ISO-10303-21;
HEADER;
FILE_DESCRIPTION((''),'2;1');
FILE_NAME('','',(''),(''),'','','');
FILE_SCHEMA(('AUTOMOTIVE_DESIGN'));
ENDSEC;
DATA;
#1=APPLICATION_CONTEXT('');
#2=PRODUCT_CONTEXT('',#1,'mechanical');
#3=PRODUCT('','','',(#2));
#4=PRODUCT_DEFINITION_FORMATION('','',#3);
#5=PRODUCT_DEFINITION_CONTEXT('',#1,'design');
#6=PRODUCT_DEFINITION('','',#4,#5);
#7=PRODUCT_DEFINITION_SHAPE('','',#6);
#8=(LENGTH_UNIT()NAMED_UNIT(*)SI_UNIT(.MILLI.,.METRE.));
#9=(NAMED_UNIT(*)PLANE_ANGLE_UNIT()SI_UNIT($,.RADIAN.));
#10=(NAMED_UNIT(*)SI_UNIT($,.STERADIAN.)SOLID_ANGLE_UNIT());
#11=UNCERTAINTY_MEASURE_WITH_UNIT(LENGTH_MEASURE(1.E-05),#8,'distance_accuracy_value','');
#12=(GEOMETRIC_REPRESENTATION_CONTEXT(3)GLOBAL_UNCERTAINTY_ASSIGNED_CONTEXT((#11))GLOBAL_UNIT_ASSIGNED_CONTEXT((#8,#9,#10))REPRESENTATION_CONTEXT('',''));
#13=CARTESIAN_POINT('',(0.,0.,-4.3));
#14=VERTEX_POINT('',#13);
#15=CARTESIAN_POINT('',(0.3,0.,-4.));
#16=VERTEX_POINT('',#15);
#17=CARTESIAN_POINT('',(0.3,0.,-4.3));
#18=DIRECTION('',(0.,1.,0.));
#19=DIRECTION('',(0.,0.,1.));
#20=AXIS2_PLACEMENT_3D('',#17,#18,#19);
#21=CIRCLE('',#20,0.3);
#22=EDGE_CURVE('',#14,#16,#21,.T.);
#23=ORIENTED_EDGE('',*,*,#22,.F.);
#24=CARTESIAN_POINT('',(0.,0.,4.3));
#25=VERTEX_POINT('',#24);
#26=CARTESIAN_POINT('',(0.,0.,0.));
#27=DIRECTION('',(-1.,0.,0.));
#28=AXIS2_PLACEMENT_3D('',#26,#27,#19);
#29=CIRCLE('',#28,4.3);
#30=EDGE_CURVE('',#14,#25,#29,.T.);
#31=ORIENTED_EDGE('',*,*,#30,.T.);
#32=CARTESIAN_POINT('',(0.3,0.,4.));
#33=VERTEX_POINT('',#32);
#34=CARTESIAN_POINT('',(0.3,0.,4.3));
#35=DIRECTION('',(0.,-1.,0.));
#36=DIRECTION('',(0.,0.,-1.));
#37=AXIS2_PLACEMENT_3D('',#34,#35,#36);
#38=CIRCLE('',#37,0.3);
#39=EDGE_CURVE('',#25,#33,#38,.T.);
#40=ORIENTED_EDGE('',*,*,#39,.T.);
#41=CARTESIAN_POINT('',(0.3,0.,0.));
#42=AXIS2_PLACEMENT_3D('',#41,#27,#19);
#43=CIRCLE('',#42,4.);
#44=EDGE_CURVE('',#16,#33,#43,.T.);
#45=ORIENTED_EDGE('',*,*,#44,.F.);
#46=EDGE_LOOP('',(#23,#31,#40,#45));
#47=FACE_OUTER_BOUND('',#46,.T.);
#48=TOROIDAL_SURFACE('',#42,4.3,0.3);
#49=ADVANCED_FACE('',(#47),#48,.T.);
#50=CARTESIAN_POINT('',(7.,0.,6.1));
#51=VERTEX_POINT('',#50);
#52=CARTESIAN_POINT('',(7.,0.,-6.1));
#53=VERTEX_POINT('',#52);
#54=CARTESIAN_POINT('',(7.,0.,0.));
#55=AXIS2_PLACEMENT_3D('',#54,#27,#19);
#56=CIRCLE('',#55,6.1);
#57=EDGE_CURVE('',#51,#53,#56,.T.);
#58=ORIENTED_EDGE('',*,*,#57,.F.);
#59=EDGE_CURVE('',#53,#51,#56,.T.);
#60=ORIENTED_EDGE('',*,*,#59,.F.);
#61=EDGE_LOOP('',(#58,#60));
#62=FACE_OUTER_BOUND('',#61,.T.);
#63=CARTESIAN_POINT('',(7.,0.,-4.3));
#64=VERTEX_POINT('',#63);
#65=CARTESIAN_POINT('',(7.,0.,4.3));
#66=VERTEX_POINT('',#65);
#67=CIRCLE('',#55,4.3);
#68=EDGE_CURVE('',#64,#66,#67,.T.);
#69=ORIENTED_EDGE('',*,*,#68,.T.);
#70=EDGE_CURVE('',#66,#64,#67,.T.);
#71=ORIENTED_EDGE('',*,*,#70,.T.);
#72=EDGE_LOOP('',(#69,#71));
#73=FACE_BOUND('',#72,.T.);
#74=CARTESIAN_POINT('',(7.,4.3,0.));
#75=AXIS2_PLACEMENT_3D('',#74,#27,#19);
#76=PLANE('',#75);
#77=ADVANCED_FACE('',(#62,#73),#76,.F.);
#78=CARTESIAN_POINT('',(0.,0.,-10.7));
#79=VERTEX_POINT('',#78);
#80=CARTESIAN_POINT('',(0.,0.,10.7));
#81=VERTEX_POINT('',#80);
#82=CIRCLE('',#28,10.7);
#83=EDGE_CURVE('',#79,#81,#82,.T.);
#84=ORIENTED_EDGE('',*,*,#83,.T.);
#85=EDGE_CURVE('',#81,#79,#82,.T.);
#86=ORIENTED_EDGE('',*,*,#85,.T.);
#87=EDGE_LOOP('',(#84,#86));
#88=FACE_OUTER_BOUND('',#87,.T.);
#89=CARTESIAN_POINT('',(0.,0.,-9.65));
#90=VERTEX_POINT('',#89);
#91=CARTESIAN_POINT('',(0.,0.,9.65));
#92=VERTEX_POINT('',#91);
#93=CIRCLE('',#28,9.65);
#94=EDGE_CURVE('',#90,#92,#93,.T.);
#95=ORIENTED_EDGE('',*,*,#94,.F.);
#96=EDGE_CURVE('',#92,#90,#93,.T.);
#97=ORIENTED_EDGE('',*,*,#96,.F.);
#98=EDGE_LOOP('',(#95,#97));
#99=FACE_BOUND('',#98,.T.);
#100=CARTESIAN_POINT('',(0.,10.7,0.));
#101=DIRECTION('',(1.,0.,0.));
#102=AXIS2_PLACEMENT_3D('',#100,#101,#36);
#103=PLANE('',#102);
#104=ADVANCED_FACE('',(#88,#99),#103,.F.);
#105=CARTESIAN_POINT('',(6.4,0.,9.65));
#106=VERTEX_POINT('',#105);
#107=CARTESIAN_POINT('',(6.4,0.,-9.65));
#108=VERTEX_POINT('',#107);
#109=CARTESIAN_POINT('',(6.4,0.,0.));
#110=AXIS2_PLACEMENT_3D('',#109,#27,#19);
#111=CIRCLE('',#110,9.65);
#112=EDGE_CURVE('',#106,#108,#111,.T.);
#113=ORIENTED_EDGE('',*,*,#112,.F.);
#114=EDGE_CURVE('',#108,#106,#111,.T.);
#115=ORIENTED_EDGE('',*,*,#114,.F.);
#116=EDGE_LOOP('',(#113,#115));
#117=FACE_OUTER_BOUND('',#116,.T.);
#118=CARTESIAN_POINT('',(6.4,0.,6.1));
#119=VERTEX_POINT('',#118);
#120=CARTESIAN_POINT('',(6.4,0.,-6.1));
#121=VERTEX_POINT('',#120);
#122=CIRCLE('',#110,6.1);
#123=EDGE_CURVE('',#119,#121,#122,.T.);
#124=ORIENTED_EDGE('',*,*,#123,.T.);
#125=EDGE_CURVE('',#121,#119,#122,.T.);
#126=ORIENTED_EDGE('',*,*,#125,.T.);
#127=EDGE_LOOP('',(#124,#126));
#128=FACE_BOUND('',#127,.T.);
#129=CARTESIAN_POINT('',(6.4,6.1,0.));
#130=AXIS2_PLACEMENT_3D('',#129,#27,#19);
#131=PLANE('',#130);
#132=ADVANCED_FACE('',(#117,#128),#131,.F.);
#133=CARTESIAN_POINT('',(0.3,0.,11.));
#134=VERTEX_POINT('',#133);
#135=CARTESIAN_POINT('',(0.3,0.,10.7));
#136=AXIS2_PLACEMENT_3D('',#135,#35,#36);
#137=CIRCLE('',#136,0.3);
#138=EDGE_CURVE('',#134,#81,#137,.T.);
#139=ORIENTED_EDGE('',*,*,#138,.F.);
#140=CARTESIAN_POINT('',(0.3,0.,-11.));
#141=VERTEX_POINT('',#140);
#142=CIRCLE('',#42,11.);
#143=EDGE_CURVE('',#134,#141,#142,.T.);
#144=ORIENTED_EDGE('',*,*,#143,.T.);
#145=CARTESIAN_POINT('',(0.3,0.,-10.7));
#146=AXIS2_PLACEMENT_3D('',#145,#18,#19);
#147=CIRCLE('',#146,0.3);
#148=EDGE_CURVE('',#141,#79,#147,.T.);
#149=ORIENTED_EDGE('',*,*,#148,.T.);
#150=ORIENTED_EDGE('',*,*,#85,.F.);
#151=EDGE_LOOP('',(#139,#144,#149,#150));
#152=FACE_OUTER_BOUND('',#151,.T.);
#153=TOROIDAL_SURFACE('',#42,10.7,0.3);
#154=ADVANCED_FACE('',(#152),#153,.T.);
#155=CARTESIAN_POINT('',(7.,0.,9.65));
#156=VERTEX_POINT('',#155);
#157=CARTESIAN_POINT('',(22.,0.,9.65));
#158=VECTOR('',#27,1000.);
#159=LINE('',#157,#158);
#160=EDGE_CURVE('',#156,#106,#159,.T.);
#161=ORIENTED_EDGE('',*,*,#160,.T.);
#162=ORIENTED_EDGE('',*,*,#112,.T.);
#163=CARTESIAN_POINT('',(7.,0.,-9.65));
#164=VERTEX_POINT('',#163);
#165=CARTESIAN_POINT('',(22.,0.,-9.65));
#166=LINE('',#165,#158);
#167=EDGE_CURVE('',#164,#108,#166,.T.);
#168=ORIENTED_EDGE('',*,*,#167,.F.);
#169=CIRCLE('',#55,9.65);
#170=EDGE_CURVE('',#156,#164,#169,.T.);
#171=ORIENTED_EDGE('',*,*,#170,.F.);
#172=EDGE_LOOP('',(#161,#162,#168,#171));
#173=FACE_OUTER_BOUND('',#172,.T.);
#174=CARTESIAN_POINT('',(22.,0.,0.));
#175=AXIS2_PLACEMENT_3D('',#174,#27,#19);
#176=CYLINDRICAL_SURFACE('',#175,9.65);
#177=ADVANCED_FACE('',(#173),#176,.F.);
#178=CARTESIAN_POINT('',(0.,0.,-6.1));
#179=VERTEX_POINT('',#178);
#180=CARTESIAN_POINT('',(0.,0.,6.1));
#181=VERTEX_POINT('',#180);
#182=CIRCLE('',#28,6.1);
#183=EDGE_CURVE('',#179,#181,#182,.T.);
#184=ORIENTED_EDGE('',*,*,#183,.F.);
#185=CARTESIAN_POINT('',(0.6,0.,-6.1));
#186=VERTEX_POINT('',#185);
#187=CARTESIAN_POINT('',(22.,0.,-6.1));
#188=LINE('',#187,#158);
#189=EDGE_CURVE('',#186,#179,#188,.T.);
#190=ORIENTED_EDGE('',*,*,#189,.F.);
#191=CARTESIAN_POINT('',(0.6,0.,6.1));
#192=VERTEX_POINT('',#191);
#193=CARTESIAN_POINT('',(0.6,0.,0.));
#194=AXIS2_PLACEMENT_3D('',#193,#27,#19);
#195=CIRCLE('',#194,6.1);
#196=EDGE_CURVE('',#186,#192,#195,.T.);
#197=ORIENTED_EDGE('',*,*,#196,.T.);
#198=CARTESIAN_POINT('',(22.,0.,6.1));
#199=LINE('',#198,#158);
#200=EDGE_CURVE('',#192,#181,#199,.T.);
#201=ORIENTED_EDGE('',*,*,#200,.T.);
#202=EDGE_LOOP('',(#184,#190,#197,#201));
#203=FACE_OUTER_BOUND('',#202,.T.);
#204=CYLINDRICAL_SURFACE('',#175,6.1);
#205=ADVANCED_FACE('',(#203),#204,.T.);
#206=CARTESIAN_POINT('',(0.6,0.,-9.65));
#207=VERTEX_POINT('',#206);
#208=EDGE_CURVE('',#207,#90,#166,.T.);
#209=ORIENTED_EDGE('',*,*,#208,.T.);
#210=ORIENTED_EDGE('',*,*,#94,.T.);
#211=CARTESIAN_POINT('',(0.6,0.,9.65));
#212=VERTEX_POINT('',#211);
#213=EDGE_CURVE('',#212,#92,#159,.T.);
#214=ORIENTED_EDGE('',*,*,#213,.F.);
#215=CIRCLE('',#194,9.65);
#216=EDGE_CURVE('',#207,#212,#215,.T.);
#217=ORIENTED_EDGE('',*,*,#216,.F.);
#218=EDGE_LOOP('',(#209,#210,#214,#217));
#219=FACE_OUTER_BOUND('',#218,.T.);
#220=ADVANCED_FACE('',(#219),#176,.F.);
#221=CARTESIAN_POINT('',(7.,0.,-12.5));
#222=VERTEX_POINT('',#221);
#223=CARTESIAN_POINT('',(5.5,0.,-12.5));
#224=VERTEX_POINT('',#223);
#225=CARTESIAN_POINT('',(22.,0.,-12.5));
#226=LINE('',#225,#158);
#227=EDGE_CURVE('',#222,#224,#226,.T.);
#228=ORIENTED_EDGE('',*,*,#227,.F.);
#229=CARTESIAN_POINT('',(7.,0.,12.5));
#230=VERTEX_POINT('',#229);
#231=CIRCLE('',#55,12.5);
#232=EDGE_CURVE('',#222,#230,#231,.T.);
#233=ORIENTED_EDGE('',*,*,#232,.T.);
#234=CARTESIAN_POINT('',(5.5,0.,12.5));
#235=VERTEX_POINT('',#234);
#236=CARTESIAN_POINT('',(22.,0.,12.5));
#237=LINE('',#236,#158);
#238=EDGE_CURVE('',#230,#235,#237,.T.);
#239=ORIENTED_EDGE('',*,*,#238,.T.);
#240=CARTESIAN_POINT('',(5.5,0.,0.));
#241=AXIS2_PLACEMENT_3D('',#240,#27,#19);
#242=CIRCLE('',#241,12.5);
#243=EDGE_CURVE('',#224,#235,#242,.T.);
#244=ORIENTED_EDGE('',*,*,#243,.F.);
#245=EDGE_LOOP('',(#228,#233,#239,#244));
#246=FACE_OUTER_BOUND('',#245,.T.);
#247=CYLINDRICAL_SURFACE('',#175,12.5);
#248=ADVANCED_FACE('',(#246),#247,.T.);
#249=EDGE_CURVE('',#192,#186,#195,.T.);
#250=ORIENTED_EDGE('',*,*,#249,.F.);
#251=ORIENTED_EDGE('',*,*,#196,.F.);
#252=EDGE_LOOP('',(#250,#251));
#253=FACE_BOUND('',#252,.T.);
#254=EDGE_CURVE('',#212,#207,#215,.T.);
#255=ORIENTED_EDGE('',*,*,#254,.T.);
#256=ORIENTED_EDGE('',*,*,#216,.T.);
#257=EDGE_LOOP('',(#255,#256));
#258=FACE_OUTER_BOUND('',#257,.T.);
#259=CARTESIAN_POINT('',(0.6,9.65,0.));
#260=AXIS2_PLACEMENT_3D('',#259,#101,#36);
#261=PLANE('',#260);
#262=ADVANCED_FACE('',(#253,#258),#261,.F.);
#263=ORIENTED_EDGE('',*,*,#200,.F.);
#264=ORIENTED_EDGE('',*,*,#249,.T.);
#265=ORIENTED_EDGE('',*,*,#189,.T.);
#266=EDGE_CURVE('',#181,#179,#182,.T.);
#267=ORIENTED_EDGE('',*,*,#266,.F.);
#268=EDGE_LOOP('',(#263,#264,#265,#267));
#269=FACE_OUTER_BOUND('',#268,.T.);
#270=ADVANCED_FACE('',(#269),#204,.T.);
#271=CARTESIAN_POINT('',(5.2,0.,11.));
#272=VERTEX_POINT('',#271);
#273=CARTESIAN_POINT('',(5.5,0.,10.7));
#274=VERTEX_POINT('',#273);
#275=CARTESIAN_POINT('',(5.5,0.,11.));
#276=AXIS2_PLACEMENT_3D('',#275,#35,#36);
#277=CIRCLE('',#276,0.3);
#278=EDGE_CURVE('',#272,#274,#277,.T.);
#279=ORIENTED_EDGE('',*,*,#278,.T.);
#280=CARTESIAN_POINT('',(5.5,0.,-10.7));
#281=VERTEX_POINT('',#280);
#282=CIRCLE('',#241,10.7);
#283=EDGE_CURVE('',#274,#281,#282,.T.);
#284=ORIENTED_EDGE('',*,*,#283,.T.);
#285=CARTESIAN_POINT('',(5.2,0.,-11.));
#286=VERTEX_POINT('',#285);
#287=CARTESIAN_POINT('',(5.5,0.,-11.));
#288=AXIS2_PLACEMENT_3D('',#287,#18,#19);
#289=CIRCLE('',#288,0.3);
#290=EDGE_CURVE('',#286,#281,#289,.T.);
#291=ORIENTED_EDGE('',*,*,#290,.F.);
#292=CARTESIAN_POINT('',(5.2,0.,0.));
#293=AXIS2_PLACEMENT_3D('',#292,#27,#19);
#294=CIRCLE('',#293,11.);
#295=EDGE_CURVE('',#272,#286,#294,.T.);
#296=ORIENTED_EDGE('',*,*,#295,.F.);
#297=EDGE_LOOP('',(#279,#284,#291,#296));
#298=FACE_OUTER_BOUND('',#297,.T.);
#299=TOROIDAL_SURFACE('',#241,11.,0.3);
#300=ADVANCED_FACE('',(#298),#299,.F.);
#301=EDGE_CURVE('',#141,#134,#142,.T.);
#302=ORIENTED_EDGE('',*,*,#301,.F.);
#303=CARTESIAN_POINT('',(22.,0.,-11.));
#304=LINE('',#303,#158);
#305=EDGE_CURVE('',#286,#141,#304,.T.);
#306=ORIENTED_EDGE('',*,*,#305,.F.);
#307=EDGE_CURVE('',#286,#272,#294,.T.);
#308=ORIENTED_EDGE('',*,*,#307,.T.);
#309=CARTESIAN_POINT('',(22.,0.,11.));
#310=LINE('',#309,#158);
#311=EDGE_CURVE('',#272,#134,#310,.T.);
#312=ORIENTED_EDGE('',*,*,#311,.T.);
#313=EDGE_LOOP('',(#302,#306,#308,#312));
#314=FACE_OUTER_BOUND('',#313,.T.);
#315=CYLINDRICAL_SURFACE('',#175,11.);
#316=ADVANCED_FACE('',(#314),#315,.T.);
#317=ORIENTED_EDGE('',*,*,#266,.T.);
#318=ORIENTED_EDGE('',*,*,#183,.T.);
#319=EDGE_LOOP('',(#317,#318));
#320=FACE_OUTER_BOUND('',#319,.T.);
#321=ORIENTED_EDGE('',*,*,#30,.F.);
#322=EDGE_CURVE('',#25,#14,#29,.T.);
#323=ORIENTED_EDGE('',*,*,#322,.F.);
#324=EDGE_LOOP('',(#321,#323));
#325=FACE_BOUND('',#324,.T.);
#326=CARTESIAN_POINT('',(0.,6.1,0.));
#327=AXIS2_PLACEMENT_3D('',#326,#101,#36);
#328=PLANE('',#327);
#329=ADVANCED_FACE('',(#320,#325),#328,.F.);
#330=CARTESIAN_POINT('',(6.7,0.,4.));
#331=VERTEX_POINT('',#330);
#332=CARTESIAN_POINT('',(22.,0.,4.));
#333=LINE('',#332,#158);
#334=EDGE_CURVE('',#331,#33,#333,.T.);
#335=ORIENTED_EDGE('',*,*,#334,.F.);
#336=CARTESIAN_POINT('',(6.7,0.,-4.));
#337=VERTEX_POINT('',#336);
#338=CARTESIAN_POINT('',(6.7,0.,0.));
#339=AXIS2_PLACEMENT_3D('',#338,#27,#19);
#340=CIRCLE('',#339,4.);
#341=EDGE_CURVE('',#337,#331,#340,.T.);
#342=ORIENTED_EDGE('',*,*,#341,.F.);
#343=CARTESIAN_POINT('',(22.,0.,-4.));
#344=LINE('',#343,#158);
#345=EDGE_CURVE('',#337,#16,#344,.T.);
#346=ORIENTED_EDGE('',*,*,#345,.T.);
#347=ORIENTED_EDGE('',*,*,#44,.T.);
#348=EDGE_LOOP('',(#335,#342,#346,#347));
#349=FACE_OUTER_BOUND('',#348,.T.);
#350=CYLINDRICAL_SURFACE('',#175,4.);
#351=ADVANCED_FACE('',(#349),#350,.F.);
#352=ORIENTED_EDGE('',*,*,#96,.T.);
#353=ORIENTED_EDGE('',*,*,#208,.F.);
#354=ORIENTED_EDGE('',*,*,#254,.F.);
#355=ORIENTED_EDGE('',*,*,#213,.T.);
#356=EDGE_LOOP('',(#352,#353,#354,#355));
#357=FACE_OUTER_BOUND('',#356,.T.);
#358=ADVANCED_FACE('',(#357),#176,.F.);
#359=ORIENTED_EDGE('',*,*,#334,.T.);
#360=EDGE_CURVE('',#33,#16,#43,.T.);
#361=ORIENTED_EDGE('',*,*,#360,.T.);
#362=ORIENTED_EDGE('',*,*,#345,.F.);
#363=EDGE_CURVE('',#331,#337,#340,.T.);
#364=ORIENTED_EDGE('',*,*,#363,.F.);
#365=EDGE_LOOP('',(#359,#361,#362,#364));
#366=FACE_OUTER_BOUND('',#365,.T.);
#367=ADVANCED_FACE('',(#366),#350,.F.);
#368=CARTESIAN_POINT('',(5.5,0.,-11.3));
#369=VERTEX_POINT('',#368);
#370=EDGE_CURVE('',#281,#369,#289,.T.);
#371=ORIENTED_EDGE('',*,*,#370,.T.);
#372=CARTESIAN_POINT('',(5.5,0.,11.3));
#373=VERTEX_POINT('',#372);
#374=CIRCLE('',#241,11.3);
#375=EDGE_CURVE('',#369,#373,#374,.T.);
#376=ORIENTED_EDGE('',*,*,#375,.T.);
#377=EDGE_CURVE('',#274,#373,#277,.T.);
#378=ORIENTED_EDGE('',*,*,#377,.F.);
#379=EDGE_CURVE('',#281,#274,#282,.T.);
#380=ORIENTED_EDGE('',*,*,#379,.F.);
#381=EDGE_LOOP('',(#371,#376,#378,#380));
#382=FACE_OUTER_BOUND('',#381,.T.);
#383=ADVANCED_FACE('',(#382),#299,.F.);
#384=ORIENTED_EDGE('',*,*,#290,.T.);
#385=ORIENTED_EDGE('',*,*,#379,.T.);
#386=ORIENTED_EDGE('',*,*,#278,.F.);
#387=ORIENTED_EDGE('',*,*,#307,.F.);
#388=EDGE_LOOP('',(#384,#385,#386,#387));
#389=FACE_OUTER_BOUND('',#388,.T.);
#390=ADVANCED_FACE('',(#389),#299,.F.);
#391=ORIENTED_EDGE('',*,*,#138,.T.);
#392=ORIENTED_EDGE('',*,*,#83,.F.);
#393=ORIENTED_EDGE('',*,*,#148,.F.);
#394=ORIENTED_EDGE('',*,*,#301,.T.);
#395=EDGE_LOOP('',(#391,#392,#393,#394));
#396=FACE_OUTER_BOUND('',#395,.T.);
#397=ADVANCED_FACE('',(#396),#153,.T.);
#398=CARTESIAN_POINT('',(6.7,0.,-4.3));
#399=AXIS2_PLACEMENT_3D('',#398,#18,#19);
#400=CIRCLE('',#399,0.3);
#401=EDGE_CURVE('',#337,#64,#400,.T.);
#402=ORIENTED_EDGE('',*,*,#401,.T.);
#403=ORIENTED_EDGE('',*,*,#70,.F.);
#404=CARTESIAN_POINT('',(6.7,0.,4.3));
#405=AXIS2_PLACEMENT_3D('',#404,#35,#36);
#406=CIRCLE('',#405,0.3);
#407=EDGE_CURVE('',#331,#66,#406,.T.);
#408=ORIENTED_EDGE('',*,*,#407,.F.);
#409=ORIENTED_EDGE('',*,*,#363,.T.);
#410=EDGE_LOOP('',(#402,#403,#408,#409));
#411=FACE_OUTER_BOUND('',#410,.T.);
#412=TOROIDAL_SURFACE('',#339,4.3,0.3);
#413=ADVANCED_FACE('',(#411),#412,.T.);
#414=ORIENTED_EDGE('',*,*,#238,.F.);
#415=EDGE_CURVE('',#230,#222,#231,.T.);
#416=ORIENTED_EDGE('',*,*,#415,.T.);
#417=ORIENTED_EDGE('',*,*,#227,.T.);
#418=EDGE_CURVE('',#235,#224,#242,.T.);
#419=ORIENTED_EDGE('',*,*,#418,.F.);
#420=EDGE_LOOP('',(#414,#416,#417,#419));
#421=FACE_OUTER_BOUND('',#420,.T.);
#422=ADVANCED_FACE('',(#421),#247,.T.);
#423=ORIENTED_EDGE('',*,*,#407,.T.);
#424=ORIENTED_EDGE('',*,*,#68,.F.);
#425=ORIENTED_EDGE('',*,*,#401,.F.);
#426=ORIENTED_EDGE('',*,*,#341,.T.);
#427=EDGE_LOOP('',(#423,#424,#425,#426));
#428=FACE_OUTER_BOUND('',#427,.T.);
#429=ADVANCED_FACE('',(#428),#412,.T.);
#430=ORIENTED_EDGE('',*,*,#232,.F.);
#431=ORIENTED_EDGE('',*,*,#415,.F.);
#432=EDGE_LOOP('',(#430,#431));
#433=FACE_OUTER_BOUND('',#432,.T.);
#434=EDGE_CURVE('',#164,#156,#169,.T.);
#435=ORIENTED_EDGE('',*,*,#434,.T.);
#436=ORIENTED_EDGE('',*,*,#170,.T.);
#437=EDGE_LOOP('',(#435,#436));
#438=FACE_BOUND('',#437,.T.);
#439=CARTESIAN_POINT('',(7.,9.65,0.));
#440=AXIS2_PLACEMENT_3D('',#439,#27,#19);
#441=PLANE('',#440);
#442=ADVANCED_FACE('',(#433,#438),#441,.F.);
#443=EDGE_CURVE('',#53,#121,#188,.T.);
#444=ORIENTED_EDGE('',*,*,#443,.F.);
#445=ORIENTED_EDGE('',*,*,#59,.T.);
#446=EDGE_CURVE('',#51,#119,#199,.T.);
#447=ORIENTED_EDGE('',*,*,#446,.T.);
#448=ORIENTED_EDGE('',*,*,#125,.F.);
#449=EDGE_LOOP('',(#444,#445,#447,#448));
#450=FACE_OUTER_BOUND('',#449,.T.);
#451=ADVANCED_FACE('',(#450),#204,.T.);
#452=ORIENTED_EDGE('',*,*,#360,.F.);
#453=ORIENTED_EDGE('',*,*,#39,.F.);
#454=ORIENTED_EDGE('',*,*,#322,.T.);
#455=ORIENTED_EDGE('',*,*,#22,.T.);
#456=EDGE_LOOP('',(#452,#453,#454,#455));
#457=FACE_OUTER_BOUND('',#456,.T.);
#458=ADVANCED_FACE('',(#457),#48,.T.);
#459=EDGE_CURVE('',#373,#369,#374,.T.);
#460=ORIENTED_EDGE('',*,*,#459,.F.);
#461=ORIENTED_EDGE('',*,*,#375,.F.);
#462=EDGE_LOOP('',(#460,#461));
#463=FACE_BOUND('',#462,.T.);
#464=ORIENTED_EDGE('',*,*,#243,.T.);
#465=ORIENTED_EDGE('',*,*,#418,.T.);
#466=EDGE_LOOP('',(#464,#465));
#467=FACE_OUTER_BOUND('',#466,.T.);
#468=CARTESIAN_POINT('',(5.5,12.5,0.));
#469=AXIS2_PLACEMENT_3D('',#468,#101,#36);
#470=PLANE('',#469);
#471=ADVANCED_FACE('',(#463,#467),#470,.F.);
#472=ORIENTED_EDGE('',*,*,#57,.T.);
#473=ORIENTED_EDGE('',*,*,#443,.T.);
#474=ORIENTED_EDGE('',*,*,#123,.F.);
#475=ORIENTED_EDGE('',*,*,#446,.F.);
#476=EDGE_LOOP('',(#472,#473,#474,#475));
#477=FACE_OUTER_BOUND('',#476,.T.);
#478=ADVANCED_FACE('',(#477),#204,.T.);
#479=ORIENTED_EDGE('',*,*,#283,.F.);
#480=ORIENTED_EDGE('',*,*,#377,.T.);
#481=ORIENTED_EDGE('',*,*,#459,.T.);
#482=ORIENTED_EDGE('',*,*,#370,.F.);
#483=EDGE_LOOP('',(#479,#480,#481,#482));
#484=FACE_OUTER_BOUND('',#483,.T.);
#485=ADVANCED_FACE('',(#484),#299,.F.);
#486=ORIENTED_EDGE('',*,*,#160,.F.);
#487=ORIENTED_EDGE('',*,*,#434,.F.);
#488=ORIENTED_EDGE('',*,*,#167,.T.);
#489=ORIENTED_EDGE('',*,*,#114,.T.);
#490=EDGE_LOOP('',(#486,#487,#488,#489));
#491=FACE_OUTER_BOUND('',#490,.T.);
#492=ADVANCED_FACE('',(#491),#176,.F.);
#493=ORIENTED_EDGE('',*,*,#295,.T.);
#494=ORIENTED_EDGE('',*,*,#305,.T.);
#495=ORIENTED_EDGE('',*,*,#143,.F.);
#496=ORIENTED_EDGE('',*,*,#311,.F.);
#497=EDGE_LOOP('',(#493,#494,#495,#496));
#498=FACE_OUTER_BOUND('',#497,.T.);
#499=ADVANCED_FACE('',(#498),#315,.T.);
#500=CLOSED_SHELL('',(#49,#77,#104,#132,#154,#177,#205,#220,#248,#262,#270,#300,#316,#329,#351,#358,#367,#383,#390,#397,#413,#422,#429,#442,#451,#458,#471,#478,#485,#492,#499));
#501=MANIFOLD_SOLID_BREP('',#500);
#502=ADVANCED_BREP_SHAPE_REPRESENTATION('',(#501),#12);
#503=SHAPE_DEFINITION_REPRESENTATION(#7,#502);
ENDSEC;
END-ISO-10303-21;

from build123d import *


with BuildPart() as part:
    # Sketch1 → Revolve1 (revolve)
    with BuildSketch(Plane.XY, mode=Mode.PRIVATE) as revolve1_sk:
        with BuildLine():
            Line((0, 10.7), (0, 9.65))
            Line((0, 9.65), (0.6, 9.65))
            Line((0.6, 9.65), (0.6, 6.1))
            Line((0.6, 6.1), (0, 6.1))
            Line((0, 6.1), (0, 4.3))
            ThreePointArc((0, 4.3), (0.087867966, 4.087867966), (0.3, 4))
            Line((0.3, 4), (6.7, 4))
            ThreePointArc((6.7, 4), (6.912132034, 4.087867966), (7, 4.3))
            Line((7, 4.3), (7, 6.1))
            Line((7, 6.1), (6.4, 6.1))
            Line((6.4, 6.1), (6.4, 9.65))
            Line((6.4, 9.65), (7, 9.65))
            Line((7, 9.65), (7, 12.5))
            Line((7, 12.5), (5.5, 12.5))
            Line((5.5, 12.5), (5.5, 11.3))
            ThreePointArc((5.5, 11.3), (5.712132034, 10.787867966), (5.2, 11))
            Line((5.2, 11), (0.3, 11))
            ThreePointArc((0.3, 11), (0.087867966, 10.912132034), (0, 10.7))
        make_face()
    revolve(revolve1_sk.sketch.rotate(Axis((22, 0, 0), (-1, 0, 0)), 270), axis=Axis((22, 0, 0), (-1, 0, 0)))


solid = part.part
